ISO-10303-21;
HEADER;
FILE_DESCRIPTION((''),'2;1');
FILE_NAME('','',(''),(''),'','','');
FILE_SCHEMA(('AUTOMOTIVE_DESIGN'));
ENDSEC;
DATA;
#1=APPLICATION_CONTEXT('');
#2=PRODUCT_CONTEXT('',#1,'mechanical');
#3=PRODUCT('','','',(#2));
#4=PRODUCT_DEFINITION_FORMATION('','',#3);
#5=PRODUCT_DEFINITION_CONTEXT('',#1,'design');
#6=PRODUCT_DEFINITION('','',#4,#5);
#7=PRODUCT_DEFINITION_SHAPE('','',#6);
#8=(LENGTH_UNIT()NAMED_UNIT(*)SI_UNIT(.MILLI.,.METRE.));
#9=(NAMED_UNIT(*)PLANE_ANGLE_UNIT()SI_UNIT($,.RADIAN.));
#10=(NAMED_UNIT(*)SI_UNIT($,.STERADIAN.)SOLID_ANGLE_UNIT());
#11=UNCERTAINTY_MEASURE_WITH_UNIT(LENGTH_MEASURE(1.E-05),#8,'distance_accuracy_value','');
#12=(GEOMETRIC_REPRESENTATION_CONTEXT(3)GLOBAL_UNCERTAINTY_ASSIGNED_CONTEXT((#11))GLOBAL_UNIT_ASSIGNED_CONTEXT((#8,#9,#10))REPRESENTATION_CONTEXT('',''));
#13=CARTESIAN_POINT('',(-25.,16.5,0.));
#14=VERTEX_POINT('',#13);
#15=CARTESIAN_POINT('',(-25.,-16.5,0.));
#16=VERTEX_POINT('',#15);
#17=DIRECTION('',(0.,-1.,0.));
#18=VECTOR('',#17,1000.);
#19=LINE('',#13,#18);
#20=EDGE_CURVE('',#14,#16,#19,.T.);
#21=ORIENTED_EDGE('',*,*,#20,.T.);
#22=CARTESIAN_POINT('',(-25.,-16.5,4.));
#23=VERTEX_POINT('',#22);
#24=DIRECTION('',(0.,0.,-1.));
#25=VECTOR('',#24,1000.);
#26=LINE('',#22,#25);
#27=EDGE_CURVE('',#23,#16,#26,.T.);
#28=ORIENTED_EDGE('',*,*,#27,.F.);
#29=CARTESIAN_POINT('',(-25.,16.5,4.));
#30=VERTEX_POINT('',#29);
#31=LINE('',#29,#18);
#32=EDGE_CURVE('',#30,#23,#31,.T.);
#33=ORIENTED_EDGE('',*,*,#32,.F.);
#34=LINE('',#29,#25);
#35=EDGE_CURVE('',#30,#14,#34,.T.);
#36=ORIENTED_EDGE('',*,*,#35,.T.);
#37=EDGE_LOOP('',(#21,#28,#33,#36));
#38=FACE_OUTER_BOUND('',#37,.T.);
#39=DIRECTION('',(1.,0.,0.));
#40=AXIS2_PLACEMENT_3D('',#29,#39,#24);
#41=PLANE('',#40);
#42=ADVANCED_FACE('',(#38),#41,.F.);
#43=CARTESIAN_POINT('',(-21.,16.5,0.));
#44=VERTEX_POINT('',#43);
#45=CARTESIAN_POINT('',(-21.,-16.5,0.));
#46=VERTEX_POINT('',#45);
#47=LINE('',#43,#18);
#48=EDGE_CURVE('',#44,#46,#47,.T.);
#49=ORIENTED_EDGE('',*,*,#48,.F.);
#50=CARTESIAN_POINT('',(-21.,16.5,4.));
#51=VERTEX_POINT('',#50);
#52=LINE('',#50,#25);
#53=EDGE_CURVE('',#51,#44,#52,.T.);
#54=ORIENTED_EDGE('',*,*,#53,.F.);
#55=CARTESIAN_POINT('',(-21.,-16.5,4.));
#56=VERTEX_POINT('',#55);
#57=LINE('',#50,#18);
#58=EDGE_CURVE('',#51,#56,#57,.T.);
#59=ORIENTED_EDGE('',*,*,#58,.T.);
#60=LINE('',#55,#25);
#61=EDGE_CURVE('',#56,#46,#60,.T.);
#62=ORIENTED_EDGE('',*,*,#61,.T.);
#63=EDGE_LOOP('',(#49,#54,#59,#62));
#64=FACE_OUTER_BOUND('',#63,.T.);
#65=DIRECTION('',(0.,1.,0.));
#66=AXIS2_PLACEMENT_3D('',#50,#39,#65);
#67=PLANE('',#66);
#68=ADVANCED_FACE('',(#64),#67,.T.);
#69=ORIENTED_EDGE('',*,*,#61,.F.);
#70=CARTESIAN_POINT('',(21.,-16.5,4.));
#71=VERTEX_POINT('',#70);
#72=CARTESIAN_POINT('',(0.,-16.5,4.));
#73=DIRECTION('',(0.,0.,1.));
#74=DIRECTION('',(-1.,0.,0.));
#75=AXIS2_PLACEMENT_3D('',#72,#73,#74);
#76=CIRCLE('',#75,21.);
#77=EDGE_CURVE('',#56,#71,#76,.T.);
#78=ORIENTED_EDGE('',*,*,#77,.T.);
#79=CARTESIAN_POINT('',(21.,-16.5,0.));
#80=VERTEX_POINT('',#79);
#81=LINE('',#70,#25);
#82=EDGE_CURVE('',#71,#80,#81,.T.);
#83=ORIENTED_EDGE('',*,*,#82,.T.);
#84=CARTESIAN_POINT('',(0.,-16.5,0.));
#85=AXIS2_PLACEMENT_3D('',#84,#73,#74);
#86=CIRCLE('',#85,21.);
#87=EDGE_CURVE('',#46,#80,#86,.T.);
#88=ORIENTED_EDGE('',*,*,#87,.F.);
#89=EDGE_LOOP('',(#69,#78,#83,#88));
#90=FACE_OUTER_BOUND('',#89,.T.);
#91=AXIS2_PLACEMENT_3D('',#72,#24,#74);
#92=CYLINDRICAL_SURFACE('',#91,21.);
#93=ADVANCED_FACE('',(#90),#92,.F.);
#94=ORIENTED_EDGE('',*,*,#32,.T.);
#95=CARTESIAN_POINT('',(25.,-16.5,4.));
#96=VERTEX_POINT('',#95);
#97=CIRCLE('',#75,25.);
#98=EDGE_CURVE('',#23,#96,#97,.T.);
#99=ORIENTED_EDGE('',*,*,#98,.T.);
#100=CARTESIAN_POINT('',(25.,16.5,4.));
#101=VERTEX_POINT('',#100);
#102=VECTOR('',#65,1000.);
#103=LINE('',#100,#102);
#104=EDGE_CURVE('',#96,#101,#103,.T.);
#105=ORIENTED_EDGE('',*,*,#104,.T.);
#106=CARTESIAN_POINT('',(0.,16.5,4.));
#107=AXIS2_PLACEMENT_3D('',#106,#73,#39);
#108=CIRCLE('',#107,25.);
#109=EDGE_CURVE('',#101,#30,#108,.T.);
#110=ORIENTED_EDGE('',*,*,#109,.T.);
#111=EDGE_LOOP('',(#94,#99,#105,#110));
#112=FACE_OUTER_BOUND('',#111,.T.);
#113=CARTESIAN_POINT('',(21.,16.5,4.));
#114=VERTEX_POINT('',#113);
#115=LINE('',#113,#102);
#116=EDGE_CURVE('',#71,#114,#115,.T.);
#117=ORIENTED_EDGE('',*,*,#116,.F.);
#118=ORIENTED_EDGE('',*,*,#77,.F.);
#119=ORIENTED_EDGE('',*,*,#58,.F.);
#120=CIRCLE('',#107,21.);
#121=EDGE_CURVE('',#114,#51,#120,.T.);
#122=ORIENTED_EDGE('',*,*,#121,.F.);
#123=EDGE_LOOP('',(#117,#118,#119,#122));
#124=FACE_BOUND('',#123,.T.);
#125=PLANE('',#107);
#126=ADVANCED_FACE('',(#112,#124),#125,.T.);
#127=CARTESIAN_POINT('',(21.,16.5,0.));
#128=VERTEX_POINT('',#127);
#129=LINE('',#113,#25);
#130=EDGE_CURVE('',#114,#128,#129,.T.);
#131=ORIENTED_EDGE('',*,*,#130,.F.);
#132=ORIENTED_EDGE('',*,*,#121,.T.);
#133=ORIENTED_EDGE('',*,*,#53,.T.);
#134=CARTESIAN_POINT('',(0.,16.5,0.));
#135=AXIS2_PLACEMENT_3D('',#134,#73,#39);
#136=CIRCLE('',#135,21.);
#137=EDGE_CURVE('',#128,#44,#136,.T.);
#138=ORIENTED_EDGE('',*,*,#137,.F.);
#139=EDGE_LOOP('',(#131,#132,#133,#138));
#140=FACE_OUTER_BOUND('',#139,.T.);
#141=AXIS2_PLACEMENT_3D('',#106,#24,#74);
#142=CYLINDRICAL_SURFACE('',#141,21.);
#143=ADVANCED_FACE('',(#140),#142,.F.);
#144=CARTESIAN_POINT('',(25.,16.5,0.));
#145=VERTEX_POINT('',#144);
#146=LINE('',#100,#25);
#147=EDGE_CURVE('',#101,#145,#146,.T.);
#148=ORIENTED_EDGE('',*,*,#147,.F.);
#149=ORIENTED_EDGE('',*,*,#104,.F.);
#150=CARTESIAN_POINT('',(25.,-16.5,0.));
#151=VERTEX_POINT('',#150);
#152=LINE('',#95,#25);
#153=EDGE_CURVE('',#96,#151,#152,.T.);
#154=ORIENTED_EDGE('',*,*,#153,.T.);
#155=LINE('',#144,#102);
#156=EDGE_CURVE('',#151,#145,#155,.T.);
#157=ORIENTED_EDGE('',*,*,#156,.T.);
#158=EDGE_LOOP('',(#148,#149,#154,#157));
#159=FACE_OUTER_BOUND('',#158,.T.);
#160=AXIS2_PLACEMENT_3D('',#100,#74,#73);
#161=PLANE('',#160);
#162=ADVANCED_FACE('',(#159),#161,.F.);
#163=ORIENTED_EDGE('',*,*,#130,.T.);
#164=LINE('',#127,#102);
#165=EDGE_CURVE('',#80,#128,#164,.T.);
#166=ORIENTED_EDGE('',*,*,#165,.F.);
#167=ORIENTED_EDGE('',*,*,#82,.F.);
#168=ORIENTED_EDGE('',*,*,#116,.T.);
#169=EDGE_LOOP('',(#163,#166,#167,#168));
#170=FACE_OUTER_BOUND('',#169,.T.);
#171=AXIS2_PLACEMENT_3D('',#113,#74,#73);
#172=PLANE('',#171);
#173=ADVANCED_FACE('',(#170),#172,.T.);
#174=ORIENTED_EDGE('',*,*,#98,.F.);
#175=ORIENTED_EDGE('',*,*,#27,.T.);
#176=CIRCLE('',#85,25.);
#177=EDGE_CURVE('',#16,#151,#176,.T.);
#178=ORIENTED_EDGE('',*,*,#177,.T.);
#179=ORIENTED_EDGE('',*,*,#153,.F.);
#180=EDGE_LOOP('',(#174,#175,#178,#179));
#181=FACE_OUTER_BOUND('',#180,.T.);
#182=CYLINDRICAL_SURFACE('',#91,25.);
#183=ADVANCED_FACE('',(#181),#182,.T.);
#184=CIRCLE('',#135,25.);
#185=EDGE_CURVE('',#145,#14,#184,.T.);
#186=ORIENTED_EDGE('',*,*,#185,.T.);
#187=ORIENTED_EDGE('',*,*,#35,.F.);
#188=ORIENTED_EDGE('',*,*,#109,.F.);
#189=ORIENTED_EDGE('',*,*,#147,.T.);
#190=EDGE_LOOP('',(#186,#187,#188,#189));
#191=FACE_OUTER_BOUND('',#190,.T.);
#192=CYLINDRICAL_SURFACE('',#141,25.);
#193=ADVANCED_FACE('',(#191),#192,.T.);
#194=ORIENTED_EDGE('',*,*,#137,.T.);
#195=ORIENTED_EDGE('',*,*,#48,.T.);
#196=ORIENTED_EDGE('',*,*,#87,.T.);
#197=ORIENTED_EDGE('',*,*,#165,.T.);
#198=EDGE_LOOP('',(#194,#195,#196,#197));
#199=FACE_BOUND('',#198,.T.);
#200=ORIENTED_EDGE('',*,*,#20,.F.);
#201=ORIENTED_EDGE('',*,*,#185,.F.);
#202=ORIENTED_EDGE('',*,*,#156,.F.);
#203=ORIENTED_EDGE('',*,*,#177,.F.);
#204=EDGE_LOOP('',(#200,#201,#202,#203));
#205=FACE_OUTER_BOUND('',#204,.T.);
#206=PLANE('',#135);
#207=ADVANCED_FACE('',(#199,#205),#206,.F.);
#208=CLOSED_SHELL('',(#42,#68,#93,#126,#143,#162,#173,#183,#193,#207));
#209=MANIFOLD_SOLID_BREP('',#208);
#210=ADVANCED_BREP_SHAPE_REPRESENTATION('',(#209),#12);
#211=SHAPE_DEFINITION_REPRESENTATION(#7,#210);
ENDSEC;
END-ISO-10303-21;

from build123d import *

# Parameters (mm, degrees)
EXTRUDE_1_DEPTH = 4


with BuildPart() as part:
    # 草图1 → 凸台-拉伸1 (new body)
    with BuildSketch(Plane.XY):
        with BuildLine():
            Line((-25, 16.5), (-25, -16.5))
            ThreePointArc((-25, -16.5), (0, -41.5), (25, -16.5))
            Line((25, -16.5), (25, 16.5))
            ThreePointArc((25, 16.5), (0, 41.5), (-25, 16.5))
        make_face()
        with BuildLine():
            Line((-21, 16.5), (-21, -16.5))
            ThreePointArc((-21, -16.5), (0, -37.5), (21, -16.5))
            Line((21, -16.5), (21, 16.5))
            ThreePointArc((21, 16.5), (0, 37.5), (-21, 16.5))
        make_face(mode=Mode.SUBTRACT)
    extrude(amount=EXTRUDE_1_DEPTH)


solid = part.part
